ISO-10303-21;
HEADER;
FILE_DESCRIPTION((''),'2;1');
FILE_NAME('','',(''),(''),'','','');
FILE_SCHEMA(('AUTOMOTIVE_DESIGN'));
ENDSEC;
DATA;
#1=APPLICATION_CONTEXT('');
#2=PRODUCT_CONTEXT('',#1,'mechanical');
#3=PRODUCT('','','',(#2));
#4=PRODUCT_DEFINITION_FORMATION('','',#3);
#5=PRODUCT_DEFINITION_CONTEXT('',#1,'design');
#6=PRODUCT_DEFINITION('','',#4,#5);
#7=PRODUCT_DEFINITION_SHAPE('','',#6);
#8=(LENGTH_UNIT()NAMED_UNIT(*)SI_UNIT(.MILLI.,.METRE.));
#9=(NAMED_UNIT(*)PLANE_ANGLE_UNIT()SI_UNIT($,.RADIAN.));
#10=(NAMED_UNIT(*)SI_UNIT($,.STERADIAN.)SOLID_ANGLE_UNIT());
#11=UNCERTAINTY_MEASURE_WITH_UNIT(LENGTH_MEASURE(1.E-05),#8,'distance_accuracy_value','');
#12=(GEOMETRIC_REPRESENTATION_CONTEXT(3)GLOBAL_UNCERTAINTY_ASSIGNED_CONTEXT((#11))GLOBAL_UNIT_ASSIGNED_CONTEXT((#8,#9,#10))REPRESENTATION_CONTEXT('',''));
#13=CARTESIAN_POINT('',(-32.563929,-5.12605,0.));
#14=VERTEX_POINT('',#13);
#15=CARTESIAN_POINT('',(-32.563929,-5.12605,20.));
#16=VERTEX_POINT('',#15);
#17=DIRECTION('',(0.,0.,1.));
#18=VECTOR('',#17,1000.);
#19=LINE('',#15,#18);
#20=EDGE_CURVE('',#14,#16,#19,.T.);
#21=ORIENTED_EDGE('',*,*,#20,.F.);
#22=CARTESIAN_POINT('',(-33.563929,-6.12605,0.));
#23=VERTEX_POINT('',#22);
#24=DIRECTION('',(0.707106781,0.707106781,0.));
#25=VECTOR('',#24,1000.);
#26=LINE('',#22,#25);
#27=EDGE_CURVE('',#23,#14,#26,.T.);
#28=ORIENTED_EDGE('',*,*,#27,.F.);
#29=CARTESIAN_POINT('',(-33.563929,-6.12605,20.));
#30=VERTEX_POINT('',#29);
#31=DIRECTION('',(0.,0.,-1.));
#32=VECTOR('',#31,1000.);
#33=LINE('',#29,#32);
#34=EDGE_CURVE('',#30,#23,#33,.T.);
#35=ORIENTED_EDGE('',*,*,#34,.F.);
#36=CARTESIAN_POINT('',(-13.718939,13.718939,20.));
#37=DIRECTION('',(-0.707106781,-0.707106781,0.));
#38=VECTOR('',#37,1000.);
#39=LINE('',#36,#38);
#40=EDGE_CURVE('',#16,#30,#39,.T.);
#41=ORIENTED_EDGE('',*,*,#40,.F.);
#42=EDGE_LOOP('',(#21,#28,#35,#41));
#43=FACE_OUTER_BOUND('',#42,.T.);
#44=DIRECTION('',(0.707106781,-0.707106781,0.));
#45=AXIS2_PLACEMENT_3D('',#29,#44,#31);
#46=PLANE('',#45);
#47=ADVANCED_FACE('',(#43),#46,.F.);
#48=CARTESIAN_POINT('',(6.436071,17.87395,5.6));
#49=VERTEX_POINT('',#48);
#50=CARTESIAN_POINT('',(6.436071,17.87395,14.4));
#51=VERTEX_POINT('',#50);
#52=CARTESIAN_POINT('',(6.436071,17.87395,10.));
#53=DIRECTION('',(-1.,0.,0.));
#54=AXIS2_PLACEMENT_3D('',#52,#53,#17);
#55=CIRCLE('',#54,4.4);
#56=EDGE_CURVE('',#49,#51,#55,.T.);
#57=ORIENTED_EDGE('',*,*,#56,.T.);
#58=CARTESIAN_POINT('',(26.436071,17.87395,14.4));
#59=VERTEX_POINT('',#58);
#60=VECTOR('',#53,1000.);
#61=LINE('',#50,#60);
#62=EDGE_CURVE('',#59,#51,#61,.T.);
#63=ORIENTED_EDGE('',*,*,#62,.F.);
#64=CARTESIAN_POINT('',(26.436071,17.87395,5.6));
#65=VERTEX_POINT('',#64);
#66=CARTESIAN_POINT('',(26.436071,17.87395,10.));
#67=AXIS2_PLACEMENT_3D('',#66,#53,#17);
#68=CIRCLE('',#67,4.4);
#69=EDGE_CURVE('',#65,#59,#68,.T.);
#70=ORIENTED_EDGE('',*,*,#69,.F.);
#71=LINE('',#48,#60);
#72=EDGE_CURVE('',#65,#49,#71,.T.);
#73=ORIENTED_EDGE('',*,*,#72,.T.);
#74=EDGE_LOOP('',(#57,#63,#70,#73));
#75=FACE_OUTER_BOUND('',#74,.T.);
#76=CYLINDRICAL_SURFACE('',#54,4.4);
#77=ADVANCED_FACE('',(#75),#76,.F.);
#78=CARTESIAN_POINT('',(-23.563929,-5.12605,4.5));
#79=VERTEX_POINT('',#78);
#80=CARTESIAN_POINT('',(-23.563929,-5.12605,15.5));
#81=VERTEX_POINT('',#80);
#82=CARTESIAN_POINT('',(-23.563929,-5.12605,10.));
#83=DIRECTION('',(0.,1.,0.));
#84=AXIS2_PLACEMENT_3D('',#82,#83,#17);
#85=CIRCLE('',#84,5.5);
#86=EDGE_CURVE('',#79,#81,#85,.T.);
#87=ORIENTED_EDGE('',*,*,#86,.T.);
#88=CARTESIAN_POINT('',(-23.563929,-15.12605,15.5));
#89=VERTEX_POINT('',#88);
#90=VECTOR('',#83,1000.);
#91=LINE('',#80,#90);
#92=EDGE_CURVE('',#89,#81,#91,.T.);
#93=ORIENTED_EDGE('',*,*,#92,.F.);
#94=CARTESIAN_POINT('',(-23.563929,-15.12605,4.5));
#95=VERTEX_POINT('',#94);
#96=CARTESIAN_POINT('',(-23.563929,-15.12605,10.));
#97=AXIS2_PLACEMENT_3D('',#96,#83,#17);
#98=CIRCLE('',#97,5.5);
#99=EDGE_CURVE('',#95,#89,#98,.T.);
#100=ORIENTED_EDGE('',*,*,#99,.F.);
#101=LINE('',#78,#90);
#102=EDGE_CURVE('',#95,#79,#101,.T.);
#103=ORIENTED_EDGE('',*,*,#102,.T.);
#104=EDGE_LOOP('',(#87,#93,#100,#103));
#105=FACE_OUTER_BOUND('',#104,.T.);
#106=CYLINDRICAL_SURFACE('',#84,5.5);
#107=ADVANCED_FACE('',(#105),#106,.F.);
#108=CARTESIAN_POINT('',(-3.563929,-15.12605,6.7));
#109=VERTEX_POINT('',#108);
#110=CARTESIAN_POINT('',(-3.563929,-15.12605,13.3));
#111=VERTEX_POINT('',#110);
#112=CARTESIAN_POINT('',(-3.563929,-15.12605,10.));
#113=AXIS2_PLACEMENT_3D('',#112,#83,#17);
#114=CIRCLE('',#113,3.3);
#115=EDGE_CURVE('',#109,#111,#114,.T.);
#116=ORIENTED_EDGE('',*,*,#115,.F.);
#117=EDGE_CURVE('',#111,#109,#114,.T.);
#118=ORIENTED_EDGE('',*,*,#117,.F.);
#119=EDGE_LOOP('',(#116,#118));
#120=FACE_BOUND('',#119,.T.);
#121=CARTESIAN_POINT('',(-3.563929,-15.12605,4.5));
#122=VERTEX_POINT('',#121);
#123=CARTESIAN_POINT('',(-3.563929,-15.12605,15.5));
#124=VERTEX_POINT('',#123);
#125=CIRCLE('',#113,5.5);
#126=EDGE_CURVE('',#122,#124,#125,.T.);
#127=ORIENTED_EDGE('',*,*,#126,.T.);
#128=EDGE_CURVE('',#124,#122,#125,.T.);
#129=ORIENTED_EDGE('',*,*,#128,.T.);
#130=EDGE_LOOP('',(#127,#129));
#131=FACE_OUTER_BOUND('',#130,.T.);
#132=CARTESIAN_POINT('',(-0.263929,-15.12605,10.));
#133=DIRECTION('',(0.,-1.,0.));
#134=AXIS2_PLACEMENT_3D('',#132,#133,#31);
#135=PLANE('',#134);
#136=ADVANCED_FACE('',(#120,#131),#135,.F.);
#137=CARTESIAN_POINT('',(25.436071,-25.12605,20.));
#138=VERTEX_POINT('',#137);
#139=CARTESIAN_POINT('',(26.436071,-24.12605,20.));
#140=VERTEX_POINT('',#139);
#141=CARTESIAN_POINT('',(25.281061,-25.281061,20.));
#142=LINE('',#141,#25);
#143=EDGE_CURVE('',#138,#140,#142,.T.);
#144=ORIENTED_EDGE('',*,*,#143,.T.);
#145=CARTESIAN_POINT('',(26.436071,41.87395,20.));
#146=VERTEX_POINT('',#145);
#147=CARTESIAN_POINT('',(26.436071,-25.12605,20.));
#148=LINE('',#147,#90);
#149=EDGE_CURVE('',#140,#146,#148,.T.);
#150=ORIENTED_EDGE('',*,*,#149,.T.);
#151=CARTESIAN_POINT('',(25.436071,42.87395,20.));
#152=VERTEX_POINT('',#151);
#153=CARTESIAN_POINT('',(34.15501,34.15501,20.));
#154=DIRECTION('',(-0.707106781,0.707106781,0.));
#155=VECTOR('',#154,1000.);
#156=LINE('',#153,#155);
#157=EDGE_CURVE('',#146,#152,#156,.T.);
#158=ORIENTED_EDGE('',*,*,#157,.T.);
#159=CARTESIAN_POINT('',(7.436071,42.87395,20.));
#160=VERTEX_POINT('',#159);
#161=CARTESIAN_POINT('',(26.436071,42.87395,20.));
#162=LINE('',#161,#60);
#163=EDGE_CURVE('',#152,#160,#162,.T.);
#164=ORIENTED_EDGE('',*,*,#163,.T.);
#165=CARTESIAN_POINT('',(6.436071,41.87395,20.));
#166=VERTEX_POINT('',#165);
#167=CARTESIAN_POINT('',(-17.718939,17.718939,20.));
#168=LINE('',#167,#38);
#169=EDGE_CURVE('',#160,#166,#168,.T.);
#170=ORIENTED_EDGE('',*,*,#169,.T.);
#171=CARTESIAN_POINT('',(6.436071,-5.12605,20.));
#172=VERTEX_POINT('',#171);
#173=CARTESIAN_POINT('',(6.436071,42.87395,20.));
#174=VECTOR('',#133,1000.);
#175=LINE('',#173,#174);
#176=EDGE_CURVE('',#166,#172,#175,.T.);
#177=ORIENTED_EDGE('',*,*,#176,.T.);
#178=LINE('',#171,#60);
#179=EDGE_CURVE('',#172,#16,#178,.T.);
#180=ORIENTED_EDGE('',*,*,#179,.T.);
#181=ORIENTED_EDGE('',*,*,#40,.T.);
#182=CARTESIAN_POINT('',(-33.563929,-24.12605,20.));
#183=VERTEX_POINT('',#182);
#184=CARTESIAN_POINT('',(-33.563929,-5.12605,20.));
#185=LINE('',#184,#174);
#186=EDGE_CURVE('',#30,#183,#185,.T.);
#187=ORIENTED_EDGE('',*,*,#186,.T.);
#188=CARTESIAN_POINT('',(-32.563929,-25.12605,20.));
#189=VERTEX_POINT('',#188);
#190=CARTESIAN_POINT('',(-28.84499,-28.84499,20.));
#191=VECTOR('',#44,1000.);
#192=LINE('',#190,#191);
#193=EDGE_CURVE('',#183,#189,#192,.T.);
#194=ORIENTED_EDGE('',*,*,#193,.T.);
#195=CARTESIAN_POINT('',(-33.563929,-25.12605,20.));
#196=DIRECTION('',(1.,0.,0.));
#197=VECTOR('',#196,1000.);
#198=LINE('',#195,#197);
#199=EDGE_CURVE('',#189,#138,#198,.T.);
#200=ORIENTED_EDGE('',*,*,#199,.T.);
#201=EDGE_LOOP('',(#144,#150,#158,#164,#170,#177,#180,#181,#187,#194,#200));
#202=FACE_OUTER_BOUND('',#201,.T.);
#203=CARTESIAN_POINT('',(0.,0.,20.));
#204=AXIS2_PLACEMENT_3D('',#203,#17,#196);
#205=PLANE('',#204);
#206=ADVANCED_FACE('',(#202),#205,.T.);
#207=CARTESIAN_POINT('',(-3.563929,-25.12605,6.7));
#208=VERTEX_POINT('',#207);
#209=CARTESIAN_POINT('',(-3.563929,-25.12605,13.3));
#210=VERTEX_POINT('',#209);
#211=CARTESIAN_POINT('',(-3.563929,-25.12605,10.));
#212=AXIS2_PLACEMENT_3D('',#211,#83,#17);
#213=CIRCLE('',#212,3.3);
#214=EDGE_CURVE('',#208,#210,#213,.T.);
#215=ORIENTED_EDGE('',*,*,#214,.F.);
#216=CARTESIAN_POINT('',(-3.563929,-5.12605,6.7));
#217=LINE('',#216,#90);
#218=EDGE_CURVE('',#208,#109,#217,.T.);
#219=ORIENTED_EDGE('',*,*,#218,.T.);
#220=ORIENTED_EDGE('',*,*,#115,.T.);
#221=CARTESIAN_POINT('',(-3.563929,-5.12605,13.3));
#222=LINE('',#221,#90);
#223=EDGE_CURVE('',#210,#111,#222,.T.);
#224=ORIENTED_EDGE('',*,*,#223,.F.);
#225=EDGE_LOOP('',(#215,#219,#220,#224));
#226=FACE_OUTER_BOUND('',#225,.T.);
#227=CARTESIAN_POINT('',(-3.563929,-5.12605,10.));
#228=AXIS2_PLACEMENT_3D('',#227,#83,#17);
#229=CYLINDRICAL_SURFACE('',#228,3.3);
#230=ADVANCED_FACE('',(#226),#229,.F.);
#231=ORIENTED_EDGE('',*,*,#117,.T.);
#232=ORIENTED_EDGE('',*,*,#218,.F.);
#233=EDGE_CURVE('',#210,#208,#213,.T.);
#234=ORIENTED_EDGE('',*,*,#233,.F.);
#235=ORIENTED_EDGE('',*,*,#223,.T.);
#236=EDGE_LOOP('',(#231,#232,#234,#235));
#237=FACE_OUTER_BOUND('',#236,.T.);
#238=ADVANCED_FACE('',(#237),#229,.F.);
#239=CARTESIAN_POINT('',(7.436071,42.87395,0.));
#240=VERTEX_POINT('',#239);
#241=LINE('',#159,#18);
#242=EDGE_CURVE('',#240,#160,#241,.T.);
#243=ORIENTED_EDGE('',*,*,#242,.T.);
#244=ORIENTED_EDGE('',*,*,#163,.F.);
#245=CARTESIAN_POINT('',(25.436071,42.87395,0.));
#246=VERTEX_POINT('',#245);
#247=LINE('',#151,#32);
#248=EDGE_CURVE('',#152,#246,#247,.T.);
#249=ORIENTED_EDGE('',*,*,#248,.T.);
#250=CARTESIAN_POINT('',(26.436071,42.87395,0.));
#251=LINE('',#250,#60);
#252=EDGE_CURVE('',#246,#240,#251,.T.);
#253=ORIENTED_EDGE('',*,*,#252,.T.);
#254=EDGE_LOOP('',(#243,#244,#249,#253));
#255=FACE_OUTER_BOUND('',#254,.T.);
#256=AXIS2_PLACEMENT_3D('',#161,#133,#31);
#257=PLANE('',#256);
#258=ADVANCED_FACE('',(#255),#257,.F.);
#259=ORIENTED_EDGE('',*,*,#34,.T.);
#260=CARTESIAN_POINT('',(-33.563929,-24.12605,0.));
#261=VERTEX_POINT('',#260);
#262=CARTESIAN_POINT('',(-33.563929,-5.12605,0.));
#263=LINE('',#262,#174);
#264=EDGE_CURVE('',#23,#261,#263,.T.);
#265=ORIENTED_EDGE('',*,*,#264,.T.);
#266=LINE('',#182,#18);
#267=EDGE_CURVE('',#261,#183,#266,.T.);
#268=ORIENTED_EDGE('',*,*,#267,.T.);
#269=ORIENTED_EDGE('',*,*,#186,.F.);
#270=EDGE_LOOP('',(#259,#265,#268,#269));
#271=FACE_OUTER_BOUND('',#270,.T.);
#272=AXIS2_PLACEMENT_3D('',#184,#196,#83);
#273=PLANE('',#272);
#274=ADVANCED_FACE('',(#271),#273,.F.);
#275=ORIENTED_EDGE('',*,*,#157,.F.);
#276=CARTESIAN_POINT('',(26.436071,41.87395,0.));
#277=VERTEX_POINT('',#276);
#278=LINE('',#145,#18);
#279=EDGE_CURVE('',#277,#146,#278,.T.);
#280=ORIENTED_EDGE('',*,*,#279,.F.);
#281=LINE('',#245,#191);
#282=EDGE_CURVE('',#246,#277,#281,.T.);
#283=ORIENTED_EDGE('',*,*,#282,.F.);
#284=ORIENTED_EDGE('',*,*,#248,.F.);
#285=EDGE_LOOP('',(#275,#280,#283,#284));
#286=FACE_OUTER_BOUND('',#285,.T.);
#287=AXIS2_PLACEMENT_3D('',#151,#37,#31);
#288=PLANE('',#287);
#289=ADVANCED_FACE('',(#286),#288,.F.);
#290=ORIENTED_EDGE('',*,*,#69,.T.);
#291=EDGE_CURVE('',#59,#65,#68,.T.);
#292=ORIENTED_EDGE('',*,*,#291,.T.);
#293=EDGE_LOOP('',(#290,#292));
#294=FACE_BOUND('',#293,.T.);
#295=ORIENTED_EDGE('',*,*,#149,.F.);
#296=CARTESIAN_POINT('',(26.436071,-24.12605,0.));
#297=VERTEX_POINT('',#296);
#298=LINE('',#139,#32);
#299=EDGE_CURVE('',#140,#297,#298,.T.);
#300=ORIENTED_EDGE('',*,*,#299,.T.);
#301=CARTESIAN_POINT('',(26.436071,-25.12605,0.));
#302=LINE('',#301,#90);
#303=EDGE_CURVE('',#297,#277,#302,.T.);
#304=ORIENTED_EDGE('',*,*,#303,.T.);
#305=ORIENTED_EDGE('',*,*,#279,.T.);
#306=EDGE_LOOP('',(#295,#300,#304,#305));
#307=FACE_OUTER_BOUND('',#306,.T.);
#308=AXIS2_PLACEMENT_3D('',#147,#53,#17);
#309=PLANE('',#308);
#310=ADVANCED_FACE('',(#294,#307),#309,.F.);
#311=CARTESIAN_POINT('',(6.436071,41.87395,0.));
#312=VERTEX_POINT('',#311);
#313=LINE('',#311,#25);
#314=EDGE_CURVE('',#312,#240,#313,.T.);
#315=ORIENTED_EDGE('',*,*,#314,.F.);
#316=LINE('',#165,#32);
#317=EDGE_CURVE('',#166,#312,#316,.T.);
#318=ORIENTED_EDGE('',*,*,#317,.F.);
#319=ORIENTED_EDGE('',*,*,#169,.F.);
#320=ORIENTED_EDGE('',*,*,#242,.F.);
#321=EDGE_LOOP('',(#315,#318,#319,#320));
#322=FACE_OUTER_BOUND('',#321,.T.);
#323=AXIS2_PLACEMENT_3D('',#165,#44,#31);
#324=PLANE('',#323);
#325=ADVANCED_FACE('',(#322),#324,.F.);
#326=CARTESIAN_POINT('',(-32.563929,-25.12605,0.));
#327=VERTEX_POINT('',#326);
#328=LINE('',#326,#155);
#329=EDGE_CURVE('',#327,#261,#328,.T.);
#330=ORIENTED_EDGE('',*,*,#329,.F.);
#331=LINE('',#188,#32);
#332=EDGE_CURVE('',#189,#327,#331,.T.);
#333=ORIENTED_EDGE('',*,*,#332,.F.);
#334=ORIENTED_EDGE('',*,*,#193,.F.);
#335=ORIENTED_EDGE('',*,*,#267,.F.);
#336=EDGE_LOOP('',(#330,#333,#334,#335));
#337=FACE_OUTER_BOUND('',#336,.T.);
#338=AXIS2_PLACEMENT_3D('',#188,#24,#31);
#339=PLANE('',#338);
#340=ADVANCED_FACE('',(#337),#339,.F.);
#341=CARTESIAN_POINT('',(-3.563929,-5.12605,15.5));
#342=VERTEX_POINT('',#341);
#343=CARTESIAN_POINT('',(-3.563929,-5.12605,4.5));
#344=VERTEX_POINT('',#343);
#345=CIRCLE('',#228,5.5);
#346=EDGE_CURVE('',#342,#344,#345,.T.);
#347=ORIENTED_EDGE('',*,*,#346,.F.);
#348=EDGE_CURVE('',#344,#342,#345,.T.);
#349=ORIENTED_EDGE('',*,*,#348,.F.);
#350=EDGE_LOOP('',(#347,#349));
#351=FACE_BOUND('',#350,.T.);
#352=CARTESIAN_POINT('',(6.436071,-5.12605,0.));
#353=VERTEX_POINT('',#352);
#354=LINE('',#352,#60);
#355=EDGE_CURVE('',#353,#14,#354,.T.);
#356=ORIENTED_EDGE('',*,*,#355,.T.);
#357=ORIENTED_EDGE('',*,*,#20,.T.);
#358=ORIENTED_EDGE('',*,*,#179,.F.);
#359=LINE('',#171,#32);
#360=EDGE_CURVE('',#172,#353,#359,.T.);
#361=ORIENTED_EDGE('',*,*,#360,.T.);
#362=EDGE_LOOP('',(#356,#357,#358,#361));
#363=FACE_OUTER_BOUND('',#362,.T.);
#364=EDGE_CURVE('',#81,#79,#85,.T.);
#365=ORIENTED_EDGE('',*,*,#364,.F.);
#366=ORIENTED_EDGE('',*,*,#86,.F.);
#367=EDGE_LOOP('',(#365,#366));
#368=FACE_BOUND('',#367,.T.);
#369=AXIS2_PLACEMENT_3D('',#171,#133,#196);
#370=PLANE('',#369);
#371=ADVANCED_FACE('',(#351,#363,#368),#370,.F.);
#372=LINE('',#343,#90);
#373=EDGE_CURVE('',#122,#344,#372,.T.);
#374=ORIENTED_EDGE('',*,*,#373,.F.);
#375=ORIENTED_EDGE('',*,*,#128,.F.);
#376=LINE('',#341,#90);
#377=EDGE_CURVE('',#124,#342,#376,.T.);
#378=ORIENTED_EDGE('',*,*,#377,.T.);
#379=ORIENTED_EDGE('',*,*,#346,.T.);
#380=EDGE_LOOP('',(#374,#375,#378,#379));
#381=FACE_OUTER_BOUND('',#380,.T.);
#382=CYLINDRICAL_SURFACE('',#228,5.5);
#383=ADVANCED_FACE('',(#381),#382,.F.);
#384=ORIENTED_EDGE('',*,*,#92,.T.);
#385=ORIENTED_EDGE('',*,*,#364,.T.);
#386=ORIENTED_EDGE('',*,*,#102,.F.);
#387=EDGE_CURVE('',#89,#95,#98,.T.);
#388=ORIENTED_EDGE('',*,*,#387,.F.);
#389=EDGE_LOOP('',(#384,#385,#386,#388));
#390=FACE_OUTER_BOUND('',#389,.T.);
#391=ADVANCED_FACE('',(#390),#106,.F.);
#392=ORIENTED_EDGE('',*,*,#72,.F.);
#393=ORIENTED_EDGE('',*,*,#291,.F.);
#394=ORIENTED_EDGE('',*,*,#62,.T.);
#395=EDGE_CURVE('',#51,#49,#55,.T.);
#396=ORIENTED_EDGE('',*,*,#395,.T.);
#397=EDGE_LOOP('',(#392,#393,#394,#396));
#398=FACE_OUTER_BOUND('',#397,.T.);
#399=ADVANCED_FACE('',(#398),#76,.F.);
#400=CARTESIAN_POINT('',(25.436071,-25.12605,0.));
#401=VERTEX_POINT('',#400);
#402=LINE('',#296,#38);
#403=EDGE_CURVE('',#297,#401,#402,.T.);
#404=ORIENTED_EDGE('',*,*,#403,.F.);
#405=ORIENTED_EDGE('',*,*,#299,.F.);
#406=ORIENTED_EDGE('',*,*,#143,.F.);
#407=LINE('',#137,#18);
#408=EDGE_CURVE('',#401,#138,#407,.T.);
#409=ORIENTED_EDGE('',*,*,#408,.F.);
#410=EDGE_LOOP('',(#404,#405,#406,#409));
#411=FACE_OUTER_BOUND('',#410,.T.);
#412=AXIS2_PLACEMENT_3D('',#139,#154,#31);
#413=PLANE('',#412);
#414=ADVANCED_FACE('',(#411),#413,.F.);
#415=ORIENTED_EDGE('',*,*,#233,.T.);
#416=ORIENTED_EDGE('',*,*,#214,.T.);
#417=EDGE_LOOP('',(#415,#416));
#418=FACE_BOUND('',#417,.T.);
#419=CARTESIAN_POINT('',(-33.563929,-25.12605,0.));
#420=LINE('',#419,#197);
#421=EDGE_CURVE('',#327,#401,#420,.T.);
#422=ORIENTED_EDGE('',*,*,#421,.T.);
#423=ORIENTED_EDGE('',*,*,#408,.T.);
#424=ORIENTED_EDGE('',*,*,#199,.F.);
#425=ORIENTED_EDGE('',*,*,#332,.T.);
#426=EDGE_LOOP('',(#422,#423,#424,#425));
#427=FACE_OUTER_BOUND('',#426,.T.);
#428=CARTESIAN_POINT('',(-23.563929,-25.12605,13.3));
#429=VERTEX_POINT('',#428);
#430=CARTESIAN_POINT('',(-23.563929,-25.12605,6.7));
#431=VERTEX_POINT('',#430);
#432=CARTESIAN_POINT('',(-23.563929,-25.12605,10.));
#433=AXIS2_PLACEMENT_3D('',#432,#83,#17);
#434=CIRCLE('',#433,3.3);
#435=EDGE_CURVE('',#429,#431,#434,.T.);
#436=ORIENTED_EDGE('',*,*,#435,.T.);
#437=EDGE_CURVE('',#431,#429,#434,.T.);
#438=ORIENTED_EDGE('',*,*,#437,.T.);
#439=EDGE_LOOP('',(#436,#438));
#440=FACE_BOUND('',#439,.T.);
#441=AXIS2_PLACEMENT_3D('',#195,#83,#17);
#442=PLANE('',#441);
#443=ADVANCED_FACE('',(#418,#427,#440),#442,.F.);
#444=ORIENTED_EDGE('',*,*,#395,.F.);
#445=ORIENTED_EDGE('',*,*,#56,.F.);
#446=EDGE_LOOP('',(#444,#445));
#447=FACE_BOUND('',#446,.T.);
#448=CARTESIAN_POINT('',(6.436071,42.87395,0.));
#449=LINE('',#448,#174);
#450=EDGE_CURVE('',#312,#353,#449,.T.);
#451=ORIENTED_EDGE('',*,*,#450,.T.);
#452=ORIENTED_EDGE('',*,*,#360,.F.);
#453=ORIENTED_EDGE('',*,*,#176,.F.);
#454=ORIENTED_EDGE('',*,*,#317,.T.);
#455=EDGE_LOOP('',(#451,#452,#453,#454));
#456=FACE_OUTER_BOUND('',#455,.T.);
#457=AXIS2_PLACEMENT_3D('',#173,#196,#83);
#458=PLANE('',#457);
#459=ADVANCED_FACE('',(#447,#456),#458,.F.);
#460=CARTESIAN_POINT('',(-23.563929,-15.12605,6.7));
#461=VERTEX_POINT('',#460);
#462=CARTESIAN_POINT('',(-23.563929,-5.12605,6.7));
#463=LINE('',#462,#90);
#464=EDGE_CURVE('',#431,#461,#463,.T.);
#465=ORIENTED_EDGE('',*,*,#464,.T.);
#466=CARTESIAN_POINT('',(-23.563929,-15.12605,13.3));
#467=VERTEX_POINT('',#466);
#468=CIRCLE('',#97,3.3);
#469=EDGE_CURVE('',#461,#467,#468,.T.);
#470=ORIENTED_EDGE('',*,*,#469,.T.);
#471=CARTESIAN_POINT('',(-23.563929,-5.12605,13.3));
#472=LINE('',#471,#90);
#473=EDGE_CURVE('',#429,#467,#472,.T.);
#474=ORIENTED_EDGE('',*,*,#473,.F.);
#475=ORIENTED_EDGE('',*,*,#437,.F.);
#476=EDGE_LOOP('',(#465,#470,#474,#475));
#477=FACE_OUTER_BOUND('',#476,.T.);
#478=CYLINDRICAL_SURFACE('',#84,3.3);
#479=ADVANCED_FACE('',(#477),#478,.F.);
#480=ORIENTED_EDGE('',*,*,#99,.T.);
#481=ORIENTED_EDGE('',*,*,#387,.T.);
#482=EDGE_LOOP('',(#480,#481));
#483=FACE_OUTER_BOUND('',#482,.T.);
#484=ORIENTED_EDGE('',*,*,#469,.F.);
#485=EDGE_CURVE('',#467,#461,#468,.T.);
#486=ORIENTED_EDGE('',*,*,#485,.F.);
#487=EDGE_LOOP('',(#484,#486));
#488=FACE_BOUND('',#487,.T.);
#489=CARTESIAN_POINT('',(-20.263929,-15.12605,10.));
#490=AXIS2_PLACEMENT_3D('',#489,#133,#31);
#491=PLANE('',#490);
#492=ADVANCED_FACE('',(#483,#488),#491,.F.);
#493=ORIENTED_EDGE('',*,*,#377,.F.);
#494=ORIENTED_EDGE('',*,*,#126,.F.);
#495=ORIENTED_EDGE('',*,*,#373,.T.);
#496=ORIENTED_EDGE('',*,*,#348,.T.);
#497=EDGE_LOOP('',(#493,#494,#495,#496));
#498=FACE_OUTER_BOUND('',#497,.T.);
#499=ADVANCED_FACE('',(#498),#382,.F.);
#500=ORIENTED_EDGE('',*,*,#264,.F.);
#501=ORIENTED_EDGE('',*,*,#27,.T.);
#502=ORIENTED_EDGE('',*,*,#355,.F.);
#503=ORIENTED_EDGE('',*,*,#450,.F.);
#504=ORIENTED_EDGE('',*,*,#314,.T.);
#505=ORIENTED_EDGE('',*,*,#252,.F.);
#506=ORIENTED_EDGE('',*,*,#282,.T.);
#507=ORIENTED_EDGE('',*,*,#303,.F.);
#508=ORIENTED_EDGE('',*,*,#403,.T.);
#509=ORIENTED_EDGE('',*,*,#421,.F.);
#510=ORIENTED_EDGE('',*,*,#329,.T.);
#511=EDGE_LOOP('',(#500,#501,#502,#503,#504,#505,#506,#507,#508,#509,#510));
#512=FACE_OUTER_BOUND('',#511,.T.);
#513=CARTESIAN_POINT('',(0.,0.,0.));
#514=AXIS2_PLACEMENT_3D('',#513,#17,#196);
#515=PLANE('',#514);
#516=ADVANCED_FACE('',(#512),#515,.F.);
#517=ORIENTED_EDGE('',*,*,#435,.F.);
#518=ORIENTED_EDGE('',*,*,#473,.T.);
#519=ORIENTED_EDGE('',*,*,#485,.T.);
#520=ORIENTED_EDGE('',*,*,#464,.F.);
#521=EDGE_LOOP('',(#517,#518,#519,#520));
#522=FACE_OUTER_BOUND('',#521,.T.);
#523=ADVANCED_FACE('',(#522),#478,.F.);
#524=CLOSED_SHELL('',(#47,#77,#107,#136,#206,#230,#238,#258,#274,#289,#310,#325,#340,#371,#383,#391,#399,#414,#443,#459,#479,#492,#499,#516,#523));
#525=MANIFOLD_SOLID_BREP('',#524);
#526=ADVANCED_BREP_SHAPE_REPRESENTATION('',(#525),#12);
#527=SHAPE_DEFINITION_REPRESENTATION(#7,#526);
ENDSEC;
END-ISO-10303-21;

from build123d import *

# Parameters (mm, degrees)
BOSS_EXTRUDE1_DEPTH     = 20
M10X1_25_TAPPED_HOLE1_D = 8.8
HOLE1_D                 = 6.6
HOLE1_CBORE_D           = 11
HOLE1_CBORE_DEPTH       = 10
CHAMFER1_SIZE           = 1


with BuildPart() as part:
    # Sketch1 → Boss-Extrude1 (new body)
    with BuildSketch(Plane.XY):
        Polygon((6.43607117, 42.87394958), (6.43607117, -5.12605042), (-33.56392883, -5.12605042), (-33.56392883, -25.12605042), (26.43607117, -25.12605042), (26.43607117, 42.87394958), align=None)
    extrude(amount=BOSS_EXTRUDE1_DEPTH)

    # M10x1.25 Tapped Hole1 (through all)
    with Locations(Plane.ZY.offset(-6.43607117)):
        with Locations((10, 17.87394958)):
            Hole(M10X1_25_TAPPED_HOLE1_D / 2)

    # Hole1 (through all)
    with Locations(Plane(origin=(0, -5.12605042, 0), x_dir=(1, 0, 0), z_dir=(0, 1, 0))):
        with Locations((-3.56392883, -10), (-23.56392883, -10)):
            CounterBoreHole(HOLE1_D / 2, HOLE1_CBORE_D / 2, HOLE1_CBORE_DEPTH)

    # Chamfer1
    chamfer1_edges = [part.edges().sort_by_distance(p)[0] for p in [
        (26.43607117, 42.87394958, 10),
        (26.43607117, -25.12605042, 10),
        (-33.56392883, -25.12605042, 10),
        (-33.56392883, -5.12605042, 10),
        (6.43607117, 42.87394958, 10),
    ]]
    chamfer(chamfer1_edges, length=CHAMFER1_SIZE)


solid = part.part
